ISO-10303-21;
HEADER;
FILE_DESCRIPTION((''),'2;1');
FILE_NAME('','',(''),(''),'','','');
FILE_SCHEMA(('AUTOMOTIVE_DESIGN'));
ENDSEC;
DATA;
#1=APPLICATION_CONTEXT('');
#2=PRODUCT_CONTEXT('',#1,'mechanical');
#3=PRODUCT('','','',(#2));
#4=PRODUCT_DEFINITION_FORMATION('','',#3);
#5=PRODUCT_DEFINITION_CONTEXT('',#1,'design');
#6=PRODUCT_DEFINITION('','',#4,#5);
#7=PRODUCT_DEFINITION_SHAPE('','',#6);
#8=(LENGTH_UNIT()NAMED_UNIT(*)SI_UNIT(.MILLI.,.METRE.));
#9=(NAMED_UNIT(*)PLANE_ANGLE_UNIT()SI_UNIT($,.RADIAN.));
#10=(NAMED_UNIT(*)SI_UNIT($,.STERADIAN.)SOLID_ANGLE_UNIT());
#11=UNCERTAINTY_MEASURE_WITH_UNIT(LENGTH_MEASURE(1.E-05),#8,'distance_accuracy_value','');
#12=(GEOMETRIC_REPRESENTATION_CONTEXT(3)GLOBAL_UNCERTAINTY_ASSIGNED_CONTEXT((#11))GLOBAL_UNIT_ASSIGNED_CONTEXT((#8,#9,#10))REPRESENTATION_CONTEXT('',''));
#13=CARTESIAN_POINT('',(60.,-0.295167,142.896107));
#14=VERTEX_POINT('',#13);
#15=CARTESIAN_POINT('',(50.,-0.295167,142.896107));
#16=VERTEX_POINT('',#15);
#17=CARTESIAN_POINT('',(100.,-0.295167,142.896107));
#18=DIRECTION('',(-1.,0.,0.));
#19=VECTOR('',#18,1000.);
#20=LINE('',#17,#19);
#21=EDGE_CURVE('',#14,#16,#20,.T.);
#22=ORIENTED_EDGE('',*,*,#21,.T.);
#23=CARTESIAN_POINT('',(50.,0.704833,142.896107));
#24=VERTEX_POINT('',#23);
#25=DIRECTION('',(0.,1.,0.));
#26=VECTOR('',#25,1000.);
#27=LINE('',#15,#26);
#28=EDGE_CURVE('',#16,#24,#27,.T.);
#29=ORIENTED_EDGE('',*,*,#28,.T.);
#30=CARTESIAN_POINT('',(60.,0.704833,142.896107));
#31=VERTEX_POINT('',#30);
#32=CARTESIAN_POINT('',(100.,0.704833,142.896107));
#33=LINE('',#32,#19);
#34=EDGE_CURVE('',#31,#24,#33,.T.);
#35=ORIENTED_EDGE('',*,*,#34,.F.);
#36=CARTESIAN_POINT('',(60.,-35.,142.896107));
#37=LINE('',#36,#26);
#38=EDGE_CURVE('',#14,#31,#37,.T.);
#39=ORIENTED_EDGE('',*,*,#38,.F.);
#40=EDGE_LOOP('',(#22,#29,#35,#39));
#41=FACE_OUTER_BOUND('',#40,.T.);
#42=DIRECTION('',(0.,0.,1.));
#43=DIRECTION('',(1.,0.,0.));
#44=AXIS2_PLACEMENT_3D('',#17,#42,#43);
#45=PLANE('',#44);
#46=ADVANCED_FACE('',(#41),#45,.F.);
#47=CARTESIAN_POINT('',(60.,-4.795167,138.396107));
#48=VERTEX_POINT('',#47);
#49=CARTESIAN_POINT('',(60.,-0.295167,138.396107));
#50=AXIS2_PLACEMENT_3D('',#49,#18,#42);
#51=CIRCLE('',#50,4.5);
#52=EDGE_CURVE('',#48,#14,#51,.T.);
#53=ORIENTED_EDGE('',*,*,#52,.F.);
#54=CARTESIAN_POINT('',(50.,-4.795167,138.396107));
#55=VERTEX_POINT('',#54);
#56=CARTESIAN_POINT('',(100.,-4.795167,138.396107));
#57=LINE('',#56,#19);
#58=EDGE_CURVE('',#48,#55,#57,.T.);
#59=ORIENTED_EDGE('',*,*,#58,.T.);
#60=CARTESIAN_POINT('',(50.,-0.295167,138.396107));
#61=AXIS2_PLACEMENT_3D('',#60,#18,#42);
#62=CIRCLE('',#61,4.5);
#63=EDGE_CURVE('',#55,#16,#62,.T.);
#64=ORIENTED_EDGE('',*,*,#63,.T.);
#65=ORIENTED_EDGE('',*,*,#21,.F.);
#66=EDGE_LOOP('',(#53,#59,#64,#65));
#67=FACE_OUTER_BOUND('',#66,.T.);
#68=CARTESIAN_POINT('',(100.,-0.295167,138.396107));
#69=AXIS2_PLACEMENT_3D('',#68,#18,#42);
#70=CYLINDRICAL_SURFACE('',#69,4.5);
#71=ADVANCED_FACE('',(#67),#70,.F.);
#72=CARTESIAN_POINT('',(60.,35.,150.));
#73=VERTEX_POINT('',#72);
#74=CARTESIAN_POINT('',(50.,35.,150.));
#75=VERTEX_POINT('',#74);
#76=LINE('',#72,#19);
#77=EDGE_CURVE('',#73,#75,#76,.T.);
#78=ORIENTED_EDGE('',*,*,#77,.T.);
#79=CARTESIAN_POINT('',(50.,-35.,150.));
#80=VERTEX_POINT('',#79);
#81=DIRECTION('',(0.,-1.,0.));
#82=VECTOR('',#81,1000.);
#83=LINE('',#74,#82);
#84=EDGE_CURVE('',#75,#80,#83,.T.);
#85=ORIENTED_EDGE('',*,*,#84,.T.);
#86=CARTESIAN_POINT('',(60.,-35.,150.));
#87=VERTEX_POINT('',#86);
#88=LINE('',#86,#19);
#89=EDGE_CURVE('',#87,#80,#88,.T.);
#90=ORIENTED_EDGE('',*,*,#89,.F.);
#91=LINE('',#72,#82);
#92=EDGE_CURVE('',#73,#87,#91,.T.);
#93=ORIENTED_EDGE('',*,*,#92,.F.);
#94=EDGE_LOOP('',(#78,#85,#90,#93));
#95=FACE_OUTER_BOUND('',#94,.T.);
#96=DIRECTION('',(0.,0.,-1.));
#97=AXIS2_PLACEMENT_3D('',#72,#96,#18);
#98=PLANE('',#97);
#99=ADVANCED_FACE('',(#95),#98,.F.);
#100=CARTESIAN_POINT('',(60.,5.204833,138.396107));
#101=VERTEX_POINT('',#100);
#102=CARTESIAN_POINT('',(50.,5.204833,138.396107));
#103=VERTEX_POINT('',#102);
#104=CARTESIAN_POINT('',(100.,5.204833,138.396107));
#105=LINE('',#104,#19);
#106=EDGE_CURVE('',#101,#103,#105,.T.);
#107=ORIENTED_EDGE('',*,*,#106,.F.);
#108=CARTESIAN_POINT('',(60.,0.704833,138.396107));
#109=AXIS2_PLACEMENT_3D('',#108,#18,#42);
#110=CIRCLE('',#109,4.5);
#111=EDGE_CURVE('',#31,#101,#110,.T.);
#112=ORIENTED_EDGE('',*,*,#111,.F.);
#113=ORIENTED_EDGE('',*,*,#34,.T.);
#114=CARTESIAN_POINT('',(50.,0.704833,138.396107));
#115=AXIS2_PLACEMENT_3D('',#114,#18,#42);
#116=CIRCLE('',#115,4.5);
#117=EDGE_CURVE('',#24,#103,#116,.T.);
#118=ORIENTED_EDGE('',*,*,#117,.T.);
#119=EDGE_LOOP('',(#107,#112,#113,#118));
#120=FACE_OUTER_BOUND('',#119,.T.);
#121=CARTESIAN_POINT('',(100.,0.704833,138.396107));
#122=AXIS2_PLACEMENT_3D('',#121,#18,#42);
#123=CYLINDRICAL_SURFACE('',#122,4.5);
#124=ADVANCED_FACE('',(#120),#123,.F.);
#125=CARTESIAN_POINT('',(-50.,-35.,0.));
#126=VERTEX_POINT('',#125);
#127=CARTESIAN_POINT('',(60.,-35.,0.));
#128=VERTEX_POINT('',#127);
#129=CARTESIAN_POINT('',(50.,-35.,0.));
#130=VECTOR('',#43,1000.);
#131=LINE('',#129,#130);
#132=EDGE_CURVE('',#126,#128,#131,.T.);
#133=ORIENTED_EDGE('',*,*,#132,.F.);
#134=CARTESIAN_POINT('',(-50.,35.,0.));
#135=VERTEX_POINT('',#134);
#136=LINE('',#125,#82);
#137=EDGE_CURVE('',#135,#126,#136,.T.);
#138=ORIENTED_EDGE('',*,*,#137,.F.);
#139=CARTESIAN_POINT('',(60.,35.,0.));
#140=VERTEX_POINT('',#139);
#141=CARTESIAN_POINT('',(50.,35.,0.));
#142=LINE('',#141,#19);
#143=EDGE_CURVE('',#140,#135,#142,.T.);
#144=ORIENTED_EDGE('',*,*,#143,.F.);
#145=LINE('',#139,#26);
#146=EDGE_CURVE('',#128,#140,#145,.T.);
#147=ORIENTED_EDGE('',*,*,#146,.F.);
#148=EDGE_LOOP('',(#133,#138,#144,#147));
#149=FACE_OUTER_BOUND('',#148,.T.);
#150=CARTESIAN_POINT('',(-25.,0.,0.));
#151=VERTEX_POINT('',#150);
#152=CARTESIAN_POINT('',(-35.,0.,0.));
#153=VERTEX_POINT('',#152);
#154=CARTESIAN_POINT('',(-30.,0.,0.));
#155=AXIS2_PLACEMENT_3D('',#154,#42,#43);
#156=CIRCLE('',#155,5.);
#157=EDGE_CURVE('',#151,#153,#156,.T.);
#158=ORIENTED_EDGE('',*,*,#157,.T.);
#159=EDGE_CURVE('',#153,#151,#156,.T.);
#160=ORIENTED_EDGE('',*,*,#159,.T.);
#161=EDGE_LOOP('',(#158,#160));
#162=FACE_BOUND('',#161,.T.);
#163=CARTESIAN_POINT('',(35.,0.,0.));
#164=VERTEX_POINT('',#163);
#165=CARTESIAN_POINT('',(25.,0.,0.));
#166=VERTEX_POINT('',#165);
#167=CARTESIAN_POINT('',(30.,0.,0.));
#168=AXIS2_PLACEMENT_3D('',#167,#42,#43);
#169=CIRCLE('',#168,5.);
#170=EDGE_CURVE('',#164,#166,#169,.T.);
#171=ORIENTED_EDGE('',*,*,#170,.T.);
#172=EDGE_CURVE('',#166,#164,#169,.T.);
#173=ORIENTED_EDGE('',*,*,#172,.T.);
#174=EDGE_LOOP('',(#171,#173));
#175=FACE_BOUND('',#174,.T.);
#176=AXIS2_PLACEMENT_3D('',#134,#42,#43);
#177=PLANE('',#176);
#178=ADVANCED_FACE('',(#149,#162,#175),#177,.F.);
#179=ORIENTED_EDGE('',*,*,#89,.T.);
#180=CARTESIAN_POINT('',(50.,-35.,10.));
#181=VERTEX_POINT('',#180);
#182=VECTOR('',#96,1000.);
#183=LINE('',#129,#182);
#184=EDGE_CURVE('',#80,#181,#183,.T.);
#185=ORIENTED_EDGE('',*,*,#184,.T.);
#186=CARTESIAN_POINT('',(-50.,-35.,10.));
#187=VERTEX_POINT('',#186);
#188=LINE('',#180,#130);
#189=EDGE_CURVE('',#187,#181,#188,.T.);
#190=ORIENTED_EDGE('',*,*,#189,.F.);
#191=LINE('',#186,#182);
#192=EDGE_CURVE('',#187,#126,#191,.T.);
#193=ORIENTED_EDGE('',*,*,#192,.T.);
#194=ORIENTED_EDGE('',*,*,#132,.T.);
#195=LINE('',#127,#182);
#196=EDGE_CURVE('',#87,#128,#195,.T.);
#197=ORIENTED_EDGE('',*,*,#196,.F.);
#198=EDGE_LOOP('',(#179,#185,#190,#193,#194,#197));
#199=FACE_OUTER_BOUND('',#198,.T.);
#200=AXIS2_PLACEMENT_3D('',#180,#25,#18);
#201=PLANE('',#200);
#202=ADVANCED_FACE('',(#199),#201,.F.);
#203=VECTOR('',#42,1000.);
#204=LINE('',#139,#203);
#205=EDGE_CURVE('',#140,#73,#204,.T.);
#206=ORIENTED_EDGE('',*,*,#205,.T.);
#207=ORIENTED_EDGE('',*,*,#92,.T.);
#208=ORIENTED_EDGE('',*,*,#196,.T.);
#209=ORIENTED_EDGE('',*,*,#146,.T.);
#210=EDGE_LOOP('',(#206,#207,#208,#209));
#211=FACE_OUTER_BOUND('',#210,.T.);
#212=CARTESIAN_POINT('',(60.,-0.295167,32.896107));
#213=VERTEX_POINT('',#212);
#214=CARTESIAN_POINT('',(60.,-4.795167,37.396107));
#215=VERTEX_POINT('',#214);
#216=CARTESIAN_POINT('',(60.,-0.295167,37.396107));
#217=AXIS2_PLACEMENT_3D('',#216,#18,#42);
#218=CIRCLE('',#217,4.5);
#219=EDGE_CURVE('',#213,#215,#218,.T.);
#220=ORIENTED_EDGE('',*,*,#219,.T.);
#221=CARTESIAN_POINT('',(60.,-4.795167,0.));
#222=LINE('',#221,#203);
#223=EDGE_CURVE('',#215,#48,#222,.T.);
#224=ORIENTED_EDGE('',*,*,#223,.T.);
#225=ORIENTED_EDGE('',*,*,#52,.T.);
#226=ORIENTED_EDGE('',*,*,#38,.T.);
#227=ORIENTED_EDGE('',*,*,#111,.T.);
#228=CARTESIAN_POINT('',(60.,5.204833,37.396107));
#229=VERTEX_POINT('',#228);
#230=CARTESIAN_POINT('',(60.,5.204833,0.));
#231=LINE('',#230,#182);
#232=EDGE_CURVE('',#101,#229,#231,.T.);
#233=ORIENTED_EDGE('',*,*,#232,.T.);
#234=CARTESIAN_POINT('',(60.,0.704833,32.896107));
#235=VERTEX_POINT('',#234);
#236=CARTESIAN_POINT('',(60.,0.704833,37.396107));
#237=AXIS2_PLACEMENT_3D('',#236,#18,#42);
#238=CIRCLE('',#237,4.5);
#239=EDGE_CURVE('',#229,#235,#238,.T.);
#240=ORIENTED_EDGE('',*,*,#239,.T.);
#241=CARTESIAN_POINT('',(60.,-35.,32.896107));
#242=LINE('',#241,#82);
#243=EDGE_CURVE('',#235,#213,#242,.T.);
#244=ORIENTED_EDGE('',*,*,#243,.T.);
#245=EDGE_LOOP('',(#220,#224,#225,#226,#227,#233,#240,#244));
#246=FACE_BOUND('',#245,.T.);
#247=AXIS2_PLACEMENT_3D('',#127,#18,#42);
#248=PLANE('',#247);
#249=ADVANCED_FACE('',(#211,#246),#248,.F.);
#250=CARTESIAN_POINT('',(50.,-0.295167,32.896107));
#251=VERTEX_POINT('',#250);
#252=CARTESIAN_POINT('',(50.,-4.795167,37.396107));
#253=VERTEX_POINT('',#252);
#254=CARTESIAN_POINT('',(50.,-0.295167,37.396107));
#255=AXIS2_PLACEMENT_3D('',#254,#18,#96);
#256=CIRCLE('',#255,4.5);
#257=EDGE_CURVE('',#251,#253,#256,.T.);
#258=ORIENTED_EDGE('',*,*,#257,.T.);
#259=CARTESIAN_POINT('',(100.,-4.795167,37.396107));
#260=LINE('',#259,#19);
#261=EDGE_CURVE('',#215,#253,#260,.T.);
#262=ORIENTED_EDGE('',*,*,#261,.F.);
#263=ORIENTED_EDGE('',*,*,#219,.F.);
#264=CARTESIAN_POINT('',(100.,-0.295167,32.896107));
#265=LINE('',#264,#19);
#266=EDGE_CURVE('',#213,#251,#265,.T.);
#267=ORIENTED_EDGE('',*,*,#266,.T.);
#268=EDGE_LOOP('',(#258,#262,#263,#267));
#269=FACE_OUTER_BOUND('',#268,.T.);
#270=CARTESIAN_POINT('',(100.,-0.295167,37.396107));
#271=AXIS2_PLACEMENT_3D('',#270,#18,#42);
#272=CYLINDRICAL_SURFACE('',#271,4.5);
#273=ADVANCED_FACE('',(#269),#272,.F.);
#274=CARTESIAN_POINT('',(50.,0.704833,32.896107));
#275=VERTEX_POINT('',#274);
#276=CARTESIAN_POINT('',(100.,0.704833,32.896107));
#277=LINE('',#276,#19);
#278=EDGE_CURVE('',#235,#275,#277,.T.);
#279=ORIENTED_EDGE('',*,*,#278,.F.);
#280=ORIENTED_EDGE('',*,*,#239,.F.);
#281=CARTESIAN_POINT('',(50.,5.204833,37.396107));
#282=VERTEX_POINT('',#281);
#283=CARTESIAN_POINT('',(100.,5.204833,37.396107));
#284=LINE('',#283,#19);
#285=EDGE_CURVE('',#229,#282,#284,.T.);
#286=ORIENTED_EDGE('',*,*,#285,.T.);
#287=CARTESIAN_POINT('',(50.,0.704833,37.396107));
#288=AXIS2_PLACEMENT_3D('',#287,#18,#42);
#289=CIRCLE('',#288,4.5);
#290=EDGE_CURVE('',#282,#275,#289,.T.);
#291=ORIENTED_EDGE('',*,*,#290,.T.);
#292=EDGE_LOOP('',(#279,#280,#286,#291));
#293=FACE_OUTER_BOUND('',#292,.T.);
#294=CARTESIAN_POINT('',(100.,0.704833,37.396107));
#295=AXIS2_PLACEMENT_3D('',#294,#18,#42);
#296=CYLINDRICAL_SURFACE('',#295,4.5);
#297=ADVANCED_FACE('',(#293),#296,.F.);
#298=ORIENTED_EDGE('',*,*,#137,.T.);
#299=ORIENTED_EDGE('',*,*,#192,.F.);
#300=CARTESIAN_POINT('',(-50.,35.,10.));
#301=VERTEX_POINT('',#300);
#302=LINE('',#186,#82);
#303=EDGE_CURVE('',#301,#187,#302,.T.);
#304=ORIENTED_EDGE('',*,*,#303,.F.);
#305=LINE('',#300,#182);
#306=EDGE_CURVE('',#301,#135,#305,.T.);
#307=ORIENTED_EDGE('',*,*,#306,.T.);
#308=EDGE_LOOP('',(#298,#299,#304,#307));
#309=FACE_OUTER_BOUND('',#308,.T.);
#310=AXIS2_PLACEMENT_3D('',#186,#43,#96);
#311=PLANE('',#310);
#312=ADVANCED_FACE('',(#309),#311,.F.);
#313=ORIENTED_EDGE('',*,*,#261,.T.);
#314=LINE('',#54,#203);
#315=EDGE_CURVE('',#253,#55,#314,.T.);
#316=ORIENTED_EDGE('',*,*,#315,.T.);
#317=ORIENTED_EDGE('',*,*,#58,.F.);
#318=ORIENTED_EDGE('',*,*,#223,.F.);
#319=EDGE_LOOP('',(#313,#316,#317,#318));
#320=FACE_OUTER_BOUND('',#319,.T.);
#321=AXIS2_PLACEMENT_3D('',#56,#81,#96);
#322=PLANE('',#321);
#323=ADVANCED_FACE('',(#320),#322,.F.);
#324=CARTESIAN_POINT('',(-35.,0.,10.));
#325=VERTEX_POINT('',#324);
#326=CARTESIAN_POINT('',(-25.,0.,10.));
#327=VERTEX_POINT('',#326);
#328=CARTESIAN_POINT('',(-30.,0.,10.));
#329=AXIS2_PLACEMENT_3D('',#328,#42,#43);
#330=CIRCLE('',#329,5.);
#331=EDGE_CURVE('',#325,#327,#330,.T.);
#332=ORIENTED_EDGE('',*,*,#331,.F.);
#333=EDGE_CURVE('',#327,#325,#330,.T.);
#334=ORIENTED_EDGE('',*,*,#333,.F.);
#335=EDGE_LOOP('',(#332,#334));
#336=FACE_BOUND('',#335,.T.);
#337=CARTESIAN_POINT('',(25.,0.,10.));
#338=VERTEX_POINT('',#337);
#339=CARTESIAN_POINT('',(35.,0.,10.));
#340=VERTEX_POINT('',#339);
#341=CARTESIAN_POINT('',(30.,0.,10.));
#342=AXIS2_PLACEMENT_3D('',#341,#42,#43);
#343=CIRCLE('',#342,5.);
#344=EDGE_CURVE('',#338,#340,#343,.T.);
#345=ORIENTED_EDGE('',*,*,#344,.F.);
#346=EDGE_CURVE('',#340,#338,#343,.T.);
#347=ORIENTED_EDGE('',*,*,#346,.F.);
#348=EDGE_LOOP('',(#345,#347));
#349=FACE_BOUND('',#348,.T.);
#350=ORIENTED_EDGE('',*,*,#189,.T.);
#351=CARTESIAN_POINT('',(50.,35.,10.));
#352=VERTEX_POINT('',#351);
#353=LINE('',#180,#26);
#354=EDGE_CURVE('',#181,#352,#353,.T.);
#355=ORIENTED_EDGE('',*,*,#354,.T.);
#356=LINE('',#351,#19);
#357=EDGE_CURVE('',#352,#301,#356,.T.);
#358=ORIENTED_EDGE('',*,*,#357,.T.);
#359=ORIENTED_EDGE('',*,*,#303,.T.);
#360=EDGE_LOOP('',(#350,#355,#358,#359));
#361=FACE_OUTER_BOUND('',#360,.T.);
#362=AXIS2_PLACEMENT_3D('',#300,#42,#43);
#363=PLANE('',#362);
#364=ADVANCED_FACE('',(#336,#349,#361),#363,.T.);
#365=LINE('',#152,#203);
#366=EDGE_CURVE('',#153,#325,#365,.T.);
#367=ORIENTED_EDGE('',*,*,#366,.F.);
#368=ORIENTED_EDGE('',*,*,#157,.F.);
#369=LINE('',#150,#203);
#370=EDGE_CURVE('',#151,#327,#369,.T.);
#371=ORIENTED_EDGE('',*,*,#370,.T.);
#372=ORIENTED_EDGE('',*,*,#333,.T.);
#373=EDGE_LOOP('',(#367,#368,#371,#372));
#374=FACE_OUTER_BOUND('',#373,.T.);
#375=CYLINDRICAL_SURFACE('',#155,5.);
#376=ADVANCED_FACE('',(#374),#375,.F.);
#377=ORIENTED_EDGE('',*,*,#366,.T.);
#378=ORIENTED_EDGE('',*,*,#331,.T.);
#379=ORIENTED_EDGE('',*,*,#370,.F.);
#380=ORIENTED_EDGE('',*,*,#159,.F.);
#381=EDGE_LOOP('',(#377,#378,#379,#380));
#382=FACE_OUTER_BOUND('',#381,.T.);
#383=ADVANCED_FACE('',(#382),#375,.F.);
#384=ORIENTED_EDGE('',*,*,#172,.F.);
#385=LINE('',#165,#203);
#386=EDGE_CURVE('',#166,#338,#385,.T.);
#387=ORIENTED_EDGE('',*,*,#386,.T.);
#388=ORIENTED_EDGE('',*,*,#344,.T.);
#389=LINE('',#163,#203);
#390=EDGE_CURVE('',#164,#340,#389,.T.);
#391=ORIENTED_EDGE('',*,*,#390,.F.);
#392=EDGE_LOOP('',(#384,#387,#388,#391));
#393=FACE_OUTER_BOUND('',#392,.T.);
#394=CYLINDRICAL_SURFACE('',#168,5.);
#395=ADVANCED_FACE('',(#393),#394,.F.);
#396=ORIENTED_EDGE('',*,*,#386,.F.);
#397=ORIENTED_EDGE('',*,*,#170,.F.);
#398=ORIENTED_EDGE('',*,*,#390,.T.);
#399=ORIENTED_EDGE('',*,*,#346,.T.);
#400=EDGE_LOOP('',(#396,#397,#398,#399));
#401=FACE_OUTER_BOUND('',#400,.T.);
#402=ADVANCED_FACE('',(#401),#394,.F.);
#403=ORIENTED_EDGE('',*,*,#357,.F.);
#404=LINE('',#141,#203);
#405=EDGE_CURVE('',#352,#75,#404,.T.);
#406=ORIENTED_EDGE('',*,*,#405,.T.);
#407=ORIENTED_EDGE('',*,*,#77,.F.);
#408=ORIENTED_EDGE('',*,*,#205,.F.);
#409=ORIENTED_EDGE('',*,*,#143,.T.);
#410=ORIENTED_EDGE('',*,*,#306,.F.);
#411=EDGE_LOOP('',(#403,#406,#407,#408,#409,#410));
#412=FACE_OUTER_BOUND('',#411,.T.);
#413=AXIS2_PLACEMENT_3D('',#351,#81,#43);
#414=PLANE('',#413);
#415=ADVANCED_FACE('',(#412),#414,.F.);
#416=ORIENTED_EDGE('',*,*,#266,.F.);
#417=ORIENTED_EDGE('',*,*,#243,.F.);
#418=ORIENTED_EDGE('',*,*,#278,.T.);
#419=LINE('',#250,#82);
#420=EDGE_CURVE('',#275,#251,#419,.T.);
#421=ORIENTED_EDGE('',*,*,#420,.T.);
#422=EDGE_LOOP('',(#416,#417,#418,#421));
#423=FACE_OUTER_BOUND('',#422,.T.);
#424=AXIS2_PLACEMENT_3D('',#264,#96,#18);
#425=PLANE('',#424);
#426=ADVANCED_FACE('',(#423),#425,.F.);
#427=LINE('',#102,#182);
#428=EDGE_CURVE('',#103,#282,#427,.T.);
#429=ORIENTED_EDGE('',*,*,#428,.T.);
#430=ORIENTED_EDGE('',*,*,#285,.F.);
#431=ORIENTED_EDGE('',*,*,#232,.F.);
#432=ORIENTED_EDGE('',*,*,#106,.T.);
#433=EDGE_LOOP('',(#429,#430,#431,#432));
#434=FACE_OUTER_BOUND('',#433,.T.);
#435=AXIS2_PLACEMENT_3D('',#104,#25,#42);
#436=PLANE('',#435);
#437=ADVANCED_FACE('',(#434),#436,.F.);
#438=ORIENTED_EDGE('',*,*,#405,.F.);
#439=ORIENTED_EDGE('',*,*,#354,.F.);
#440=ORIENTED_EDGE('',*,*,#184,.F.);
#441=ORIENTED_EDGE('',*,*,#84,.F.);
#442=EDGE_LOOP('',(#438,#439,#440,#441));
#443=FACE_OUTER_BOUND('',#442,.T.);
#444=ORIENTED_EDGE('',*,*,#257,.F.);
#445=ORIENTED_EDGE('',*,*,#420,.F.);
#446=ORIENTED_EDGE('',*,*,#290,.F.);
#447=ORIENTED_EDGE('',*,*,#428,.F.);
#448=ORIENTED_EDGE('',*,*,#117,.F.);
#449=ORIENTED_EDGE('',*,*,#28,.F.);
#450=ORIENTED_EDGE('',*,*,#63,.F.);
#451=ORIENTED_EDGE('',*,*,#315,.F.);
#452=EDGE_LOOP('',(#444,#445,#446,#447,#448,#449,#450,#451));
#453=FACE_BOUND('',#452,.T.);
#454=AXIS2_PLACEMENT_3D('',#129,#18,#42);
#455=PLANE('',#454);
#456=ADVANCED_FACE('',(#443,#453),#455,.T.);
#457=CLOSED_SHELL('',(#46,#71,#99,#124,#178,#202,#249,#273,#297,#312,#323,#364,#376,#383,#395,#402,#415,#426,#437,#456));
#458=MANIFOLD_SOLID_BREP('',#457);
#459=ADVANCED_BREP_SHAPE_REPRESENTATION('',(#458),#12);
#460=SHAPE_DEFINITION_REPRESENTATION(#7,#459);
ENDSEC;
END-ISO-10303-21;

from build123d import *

# Parameters (mm, degrees)
SKETCH1_W           = 100
SKETCH1_H           = 70
BOSS_EXTRUDE1_DEPTH = 10
SKETCH2_R           = 5
CUT_EXTRUDE1_DEPTH  = 10
SKETCH3_W           = 150
SKETCH3_H           = 70
BOSS_EXTRUDE2_DEPTH = 10
CUT_EXTRUDE2_DEPTH  = 50


with BuildPart() as part:
    # Sketch1 → Boss-Extrude1 (new body)
    with BuildSketch(Plane.XY):
        Rectangle(SKETCH1_W, SKETCH1_H)
    extrude(amount=BOSS_EXTRUDE1_DEPTH)

    # Sketch2 → Cut-Extrude1 (cut)
    with BuildSketch(Plane.XY.offset(10)):
        with Locations((-30, 0)):
            Circle(SKETCH2_R)
        with Locations((30, 0)):
            Circle(SKETCH2_R)
    extrude(amount=-CUT_EXTRUDE1_DEPTH, mode=Mode.SUBTRACT)

    # Sketch3 → Boss-Extrude2 (add)
    with BuildSketch(Plane(origin=(50, 0, 0), x_dir=(0, 0, -1), z_dir=(1, 0, 0))):
        with Locations((-75, 0)):
            Rectangle(SKETCH3_W, SKETCH3_H)
    extrude(amount=BOSS_EXTRUDE2_DEPTH)

    # Sketch7 → Cut-Extrude2 (cut)
    with BuildSketch(Plane.ZY.offset(-50)):
        with BuildLine():
            Line((138.396107193, -4.795166993), (37.396107193, -4.795166993))
            ThreePointArc((37.396107193, -4.795166993), (34.214126678, -3.477147509), (32.896107193, -0.295166993))
            Line((32.896107193, -0.295166993), (32.896107193, 0.704833007))
            ThreePointArc((32.896107193, 0.704833007), (34.214126678, 3.886813522), (37.396107193, 5.204833007))
            Line((37.396107193, 5.204833007), (138.396107193, 5.204833007))
            ThreePointArc((138.396107193, 5.204833007), (141.578087709, 3.886813522), (142.896107193, 0.704833007))
            Line((142.896107193, 0.704833007), (142.896107193, -0.295166993))
            ThreePointArc((142.896107193, -0.295166993), (141.578087709, -3.477147509), (138.396107193, -4.795166993))
        make_face()
    extrude(amount=-CUT_EXTRUDE2_DEPTH, mode=Mode.SUBTRACT)


solid = part.part
